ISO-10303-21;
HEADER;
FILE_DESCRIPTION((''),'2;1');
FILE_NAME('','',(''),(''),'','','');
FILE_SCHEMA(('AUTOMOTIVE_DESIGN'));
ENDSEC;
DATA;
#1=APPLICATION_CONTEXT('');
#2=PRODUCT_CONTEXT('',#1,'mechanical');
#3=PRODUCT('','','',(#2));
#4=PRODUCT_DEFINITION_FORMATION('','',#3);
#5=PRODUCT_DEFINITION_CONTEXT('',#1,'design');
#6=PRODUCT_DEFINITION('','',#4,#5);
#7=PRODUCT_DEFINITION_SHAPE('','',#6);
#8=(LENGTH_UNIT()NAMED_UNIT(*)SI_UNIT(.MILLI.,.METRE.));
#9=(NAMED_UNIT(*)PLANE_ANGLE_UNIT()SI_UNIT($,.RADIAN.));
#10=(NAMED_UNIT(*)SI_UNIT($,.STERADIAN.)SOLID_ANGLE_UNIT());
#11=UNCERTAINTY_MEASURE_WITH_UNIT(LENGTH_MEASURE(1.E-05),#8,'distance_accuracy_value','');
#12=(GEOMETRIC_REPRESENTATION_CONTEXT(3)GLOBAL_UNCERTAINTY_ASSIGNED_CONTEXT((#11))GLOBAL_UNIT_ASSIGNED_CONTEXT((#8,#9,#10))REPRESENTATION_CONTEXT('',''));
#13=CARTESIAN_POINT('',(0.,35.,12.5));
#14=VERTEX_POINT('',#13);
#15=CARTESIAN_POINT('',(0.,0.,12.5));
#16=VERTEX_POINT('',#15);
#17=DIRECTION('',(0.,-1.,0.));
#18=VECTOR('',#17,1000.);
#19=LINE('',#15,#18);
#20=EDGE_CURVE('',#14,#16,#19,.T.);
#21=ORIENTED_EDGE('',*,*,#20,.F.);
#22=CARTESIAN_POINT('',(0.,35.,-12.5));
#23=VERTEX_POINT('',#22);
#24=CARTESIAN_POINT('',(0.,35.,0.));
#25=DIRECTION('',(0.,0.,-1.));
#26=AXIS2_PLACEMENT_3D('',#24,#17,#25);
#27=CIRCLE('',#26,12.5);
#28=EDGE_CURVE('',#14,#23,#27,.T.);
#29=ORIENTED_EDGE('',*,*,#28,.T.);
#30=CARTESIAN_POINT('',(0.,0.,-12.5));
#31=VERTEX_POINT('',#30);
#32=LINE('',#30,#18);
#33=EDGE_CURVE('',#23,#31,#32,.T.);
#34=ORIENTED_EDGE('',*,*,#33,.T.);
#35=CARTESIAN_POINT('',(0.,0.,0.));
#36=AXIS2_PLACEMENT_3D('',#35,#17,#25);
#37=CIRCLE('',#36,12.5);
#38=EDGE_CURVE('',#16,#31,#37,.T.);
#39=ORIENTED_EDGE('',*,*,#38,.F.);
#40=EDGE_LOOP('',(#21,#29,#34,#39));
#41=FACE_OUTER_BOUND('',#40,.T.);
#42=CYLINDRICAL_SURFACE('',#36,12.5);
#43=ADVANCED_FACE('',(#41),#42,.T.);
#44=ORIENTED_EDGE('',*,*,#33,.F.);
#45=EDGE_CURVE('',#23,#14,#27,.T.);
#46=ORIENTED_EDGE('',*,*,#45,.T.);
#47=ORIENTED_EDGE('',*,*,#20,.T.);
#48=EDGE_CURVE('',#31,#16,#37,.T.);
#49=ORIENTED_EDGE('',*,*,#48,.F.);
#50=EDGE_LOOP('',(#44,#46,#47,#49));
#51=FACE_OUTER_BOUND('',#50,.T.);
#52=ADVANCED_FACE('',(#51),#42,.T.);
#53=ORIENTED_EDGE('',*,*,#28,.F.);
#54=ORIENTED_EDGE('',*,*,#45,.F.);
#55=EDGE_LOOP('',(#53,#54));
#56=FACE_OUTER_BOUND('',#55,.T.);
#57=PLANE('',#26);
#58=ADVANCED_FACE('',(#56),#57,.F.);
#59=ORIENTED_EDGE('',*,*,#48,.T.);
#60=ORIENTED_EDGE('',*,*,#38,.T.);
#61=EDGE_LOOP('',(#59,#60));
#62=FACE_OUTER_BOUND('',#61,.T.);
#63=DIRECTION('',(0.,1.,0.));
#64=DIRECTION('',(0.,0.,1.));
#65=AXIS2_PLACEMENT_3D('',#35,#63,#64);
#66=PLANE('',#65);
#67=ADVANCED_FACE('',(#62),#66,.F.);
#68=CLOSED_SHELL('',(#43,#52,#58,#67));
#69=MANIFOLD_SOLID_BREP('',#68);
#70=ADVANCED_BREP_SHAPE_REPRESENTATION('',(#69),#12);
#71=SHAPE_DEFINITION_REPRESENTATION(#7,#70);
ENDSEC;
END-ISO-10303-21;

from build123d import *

# Parameters (mm, degrees)
SKETCH_1_W = 12.5
SKETCH_1_H = 35


with BuildPart() as part:
    # 草图1 → 旋转1 (revolve)
    with BuildSketch(Plane.XY, mode=Mode.PRIVATE) as revolve_1_sk:
        with Locations((-6.25, 17.5)):
            Rectangle(SKETCH_1_W, SKETCH_1_H)
    revolve(revolve_1_sk.sketch.rotate(Axis((0, 0, 0), (0, 1, 0)), 270), axis=Axis((0, 0, 0), (0, 1, 0)))


solid = part.part
